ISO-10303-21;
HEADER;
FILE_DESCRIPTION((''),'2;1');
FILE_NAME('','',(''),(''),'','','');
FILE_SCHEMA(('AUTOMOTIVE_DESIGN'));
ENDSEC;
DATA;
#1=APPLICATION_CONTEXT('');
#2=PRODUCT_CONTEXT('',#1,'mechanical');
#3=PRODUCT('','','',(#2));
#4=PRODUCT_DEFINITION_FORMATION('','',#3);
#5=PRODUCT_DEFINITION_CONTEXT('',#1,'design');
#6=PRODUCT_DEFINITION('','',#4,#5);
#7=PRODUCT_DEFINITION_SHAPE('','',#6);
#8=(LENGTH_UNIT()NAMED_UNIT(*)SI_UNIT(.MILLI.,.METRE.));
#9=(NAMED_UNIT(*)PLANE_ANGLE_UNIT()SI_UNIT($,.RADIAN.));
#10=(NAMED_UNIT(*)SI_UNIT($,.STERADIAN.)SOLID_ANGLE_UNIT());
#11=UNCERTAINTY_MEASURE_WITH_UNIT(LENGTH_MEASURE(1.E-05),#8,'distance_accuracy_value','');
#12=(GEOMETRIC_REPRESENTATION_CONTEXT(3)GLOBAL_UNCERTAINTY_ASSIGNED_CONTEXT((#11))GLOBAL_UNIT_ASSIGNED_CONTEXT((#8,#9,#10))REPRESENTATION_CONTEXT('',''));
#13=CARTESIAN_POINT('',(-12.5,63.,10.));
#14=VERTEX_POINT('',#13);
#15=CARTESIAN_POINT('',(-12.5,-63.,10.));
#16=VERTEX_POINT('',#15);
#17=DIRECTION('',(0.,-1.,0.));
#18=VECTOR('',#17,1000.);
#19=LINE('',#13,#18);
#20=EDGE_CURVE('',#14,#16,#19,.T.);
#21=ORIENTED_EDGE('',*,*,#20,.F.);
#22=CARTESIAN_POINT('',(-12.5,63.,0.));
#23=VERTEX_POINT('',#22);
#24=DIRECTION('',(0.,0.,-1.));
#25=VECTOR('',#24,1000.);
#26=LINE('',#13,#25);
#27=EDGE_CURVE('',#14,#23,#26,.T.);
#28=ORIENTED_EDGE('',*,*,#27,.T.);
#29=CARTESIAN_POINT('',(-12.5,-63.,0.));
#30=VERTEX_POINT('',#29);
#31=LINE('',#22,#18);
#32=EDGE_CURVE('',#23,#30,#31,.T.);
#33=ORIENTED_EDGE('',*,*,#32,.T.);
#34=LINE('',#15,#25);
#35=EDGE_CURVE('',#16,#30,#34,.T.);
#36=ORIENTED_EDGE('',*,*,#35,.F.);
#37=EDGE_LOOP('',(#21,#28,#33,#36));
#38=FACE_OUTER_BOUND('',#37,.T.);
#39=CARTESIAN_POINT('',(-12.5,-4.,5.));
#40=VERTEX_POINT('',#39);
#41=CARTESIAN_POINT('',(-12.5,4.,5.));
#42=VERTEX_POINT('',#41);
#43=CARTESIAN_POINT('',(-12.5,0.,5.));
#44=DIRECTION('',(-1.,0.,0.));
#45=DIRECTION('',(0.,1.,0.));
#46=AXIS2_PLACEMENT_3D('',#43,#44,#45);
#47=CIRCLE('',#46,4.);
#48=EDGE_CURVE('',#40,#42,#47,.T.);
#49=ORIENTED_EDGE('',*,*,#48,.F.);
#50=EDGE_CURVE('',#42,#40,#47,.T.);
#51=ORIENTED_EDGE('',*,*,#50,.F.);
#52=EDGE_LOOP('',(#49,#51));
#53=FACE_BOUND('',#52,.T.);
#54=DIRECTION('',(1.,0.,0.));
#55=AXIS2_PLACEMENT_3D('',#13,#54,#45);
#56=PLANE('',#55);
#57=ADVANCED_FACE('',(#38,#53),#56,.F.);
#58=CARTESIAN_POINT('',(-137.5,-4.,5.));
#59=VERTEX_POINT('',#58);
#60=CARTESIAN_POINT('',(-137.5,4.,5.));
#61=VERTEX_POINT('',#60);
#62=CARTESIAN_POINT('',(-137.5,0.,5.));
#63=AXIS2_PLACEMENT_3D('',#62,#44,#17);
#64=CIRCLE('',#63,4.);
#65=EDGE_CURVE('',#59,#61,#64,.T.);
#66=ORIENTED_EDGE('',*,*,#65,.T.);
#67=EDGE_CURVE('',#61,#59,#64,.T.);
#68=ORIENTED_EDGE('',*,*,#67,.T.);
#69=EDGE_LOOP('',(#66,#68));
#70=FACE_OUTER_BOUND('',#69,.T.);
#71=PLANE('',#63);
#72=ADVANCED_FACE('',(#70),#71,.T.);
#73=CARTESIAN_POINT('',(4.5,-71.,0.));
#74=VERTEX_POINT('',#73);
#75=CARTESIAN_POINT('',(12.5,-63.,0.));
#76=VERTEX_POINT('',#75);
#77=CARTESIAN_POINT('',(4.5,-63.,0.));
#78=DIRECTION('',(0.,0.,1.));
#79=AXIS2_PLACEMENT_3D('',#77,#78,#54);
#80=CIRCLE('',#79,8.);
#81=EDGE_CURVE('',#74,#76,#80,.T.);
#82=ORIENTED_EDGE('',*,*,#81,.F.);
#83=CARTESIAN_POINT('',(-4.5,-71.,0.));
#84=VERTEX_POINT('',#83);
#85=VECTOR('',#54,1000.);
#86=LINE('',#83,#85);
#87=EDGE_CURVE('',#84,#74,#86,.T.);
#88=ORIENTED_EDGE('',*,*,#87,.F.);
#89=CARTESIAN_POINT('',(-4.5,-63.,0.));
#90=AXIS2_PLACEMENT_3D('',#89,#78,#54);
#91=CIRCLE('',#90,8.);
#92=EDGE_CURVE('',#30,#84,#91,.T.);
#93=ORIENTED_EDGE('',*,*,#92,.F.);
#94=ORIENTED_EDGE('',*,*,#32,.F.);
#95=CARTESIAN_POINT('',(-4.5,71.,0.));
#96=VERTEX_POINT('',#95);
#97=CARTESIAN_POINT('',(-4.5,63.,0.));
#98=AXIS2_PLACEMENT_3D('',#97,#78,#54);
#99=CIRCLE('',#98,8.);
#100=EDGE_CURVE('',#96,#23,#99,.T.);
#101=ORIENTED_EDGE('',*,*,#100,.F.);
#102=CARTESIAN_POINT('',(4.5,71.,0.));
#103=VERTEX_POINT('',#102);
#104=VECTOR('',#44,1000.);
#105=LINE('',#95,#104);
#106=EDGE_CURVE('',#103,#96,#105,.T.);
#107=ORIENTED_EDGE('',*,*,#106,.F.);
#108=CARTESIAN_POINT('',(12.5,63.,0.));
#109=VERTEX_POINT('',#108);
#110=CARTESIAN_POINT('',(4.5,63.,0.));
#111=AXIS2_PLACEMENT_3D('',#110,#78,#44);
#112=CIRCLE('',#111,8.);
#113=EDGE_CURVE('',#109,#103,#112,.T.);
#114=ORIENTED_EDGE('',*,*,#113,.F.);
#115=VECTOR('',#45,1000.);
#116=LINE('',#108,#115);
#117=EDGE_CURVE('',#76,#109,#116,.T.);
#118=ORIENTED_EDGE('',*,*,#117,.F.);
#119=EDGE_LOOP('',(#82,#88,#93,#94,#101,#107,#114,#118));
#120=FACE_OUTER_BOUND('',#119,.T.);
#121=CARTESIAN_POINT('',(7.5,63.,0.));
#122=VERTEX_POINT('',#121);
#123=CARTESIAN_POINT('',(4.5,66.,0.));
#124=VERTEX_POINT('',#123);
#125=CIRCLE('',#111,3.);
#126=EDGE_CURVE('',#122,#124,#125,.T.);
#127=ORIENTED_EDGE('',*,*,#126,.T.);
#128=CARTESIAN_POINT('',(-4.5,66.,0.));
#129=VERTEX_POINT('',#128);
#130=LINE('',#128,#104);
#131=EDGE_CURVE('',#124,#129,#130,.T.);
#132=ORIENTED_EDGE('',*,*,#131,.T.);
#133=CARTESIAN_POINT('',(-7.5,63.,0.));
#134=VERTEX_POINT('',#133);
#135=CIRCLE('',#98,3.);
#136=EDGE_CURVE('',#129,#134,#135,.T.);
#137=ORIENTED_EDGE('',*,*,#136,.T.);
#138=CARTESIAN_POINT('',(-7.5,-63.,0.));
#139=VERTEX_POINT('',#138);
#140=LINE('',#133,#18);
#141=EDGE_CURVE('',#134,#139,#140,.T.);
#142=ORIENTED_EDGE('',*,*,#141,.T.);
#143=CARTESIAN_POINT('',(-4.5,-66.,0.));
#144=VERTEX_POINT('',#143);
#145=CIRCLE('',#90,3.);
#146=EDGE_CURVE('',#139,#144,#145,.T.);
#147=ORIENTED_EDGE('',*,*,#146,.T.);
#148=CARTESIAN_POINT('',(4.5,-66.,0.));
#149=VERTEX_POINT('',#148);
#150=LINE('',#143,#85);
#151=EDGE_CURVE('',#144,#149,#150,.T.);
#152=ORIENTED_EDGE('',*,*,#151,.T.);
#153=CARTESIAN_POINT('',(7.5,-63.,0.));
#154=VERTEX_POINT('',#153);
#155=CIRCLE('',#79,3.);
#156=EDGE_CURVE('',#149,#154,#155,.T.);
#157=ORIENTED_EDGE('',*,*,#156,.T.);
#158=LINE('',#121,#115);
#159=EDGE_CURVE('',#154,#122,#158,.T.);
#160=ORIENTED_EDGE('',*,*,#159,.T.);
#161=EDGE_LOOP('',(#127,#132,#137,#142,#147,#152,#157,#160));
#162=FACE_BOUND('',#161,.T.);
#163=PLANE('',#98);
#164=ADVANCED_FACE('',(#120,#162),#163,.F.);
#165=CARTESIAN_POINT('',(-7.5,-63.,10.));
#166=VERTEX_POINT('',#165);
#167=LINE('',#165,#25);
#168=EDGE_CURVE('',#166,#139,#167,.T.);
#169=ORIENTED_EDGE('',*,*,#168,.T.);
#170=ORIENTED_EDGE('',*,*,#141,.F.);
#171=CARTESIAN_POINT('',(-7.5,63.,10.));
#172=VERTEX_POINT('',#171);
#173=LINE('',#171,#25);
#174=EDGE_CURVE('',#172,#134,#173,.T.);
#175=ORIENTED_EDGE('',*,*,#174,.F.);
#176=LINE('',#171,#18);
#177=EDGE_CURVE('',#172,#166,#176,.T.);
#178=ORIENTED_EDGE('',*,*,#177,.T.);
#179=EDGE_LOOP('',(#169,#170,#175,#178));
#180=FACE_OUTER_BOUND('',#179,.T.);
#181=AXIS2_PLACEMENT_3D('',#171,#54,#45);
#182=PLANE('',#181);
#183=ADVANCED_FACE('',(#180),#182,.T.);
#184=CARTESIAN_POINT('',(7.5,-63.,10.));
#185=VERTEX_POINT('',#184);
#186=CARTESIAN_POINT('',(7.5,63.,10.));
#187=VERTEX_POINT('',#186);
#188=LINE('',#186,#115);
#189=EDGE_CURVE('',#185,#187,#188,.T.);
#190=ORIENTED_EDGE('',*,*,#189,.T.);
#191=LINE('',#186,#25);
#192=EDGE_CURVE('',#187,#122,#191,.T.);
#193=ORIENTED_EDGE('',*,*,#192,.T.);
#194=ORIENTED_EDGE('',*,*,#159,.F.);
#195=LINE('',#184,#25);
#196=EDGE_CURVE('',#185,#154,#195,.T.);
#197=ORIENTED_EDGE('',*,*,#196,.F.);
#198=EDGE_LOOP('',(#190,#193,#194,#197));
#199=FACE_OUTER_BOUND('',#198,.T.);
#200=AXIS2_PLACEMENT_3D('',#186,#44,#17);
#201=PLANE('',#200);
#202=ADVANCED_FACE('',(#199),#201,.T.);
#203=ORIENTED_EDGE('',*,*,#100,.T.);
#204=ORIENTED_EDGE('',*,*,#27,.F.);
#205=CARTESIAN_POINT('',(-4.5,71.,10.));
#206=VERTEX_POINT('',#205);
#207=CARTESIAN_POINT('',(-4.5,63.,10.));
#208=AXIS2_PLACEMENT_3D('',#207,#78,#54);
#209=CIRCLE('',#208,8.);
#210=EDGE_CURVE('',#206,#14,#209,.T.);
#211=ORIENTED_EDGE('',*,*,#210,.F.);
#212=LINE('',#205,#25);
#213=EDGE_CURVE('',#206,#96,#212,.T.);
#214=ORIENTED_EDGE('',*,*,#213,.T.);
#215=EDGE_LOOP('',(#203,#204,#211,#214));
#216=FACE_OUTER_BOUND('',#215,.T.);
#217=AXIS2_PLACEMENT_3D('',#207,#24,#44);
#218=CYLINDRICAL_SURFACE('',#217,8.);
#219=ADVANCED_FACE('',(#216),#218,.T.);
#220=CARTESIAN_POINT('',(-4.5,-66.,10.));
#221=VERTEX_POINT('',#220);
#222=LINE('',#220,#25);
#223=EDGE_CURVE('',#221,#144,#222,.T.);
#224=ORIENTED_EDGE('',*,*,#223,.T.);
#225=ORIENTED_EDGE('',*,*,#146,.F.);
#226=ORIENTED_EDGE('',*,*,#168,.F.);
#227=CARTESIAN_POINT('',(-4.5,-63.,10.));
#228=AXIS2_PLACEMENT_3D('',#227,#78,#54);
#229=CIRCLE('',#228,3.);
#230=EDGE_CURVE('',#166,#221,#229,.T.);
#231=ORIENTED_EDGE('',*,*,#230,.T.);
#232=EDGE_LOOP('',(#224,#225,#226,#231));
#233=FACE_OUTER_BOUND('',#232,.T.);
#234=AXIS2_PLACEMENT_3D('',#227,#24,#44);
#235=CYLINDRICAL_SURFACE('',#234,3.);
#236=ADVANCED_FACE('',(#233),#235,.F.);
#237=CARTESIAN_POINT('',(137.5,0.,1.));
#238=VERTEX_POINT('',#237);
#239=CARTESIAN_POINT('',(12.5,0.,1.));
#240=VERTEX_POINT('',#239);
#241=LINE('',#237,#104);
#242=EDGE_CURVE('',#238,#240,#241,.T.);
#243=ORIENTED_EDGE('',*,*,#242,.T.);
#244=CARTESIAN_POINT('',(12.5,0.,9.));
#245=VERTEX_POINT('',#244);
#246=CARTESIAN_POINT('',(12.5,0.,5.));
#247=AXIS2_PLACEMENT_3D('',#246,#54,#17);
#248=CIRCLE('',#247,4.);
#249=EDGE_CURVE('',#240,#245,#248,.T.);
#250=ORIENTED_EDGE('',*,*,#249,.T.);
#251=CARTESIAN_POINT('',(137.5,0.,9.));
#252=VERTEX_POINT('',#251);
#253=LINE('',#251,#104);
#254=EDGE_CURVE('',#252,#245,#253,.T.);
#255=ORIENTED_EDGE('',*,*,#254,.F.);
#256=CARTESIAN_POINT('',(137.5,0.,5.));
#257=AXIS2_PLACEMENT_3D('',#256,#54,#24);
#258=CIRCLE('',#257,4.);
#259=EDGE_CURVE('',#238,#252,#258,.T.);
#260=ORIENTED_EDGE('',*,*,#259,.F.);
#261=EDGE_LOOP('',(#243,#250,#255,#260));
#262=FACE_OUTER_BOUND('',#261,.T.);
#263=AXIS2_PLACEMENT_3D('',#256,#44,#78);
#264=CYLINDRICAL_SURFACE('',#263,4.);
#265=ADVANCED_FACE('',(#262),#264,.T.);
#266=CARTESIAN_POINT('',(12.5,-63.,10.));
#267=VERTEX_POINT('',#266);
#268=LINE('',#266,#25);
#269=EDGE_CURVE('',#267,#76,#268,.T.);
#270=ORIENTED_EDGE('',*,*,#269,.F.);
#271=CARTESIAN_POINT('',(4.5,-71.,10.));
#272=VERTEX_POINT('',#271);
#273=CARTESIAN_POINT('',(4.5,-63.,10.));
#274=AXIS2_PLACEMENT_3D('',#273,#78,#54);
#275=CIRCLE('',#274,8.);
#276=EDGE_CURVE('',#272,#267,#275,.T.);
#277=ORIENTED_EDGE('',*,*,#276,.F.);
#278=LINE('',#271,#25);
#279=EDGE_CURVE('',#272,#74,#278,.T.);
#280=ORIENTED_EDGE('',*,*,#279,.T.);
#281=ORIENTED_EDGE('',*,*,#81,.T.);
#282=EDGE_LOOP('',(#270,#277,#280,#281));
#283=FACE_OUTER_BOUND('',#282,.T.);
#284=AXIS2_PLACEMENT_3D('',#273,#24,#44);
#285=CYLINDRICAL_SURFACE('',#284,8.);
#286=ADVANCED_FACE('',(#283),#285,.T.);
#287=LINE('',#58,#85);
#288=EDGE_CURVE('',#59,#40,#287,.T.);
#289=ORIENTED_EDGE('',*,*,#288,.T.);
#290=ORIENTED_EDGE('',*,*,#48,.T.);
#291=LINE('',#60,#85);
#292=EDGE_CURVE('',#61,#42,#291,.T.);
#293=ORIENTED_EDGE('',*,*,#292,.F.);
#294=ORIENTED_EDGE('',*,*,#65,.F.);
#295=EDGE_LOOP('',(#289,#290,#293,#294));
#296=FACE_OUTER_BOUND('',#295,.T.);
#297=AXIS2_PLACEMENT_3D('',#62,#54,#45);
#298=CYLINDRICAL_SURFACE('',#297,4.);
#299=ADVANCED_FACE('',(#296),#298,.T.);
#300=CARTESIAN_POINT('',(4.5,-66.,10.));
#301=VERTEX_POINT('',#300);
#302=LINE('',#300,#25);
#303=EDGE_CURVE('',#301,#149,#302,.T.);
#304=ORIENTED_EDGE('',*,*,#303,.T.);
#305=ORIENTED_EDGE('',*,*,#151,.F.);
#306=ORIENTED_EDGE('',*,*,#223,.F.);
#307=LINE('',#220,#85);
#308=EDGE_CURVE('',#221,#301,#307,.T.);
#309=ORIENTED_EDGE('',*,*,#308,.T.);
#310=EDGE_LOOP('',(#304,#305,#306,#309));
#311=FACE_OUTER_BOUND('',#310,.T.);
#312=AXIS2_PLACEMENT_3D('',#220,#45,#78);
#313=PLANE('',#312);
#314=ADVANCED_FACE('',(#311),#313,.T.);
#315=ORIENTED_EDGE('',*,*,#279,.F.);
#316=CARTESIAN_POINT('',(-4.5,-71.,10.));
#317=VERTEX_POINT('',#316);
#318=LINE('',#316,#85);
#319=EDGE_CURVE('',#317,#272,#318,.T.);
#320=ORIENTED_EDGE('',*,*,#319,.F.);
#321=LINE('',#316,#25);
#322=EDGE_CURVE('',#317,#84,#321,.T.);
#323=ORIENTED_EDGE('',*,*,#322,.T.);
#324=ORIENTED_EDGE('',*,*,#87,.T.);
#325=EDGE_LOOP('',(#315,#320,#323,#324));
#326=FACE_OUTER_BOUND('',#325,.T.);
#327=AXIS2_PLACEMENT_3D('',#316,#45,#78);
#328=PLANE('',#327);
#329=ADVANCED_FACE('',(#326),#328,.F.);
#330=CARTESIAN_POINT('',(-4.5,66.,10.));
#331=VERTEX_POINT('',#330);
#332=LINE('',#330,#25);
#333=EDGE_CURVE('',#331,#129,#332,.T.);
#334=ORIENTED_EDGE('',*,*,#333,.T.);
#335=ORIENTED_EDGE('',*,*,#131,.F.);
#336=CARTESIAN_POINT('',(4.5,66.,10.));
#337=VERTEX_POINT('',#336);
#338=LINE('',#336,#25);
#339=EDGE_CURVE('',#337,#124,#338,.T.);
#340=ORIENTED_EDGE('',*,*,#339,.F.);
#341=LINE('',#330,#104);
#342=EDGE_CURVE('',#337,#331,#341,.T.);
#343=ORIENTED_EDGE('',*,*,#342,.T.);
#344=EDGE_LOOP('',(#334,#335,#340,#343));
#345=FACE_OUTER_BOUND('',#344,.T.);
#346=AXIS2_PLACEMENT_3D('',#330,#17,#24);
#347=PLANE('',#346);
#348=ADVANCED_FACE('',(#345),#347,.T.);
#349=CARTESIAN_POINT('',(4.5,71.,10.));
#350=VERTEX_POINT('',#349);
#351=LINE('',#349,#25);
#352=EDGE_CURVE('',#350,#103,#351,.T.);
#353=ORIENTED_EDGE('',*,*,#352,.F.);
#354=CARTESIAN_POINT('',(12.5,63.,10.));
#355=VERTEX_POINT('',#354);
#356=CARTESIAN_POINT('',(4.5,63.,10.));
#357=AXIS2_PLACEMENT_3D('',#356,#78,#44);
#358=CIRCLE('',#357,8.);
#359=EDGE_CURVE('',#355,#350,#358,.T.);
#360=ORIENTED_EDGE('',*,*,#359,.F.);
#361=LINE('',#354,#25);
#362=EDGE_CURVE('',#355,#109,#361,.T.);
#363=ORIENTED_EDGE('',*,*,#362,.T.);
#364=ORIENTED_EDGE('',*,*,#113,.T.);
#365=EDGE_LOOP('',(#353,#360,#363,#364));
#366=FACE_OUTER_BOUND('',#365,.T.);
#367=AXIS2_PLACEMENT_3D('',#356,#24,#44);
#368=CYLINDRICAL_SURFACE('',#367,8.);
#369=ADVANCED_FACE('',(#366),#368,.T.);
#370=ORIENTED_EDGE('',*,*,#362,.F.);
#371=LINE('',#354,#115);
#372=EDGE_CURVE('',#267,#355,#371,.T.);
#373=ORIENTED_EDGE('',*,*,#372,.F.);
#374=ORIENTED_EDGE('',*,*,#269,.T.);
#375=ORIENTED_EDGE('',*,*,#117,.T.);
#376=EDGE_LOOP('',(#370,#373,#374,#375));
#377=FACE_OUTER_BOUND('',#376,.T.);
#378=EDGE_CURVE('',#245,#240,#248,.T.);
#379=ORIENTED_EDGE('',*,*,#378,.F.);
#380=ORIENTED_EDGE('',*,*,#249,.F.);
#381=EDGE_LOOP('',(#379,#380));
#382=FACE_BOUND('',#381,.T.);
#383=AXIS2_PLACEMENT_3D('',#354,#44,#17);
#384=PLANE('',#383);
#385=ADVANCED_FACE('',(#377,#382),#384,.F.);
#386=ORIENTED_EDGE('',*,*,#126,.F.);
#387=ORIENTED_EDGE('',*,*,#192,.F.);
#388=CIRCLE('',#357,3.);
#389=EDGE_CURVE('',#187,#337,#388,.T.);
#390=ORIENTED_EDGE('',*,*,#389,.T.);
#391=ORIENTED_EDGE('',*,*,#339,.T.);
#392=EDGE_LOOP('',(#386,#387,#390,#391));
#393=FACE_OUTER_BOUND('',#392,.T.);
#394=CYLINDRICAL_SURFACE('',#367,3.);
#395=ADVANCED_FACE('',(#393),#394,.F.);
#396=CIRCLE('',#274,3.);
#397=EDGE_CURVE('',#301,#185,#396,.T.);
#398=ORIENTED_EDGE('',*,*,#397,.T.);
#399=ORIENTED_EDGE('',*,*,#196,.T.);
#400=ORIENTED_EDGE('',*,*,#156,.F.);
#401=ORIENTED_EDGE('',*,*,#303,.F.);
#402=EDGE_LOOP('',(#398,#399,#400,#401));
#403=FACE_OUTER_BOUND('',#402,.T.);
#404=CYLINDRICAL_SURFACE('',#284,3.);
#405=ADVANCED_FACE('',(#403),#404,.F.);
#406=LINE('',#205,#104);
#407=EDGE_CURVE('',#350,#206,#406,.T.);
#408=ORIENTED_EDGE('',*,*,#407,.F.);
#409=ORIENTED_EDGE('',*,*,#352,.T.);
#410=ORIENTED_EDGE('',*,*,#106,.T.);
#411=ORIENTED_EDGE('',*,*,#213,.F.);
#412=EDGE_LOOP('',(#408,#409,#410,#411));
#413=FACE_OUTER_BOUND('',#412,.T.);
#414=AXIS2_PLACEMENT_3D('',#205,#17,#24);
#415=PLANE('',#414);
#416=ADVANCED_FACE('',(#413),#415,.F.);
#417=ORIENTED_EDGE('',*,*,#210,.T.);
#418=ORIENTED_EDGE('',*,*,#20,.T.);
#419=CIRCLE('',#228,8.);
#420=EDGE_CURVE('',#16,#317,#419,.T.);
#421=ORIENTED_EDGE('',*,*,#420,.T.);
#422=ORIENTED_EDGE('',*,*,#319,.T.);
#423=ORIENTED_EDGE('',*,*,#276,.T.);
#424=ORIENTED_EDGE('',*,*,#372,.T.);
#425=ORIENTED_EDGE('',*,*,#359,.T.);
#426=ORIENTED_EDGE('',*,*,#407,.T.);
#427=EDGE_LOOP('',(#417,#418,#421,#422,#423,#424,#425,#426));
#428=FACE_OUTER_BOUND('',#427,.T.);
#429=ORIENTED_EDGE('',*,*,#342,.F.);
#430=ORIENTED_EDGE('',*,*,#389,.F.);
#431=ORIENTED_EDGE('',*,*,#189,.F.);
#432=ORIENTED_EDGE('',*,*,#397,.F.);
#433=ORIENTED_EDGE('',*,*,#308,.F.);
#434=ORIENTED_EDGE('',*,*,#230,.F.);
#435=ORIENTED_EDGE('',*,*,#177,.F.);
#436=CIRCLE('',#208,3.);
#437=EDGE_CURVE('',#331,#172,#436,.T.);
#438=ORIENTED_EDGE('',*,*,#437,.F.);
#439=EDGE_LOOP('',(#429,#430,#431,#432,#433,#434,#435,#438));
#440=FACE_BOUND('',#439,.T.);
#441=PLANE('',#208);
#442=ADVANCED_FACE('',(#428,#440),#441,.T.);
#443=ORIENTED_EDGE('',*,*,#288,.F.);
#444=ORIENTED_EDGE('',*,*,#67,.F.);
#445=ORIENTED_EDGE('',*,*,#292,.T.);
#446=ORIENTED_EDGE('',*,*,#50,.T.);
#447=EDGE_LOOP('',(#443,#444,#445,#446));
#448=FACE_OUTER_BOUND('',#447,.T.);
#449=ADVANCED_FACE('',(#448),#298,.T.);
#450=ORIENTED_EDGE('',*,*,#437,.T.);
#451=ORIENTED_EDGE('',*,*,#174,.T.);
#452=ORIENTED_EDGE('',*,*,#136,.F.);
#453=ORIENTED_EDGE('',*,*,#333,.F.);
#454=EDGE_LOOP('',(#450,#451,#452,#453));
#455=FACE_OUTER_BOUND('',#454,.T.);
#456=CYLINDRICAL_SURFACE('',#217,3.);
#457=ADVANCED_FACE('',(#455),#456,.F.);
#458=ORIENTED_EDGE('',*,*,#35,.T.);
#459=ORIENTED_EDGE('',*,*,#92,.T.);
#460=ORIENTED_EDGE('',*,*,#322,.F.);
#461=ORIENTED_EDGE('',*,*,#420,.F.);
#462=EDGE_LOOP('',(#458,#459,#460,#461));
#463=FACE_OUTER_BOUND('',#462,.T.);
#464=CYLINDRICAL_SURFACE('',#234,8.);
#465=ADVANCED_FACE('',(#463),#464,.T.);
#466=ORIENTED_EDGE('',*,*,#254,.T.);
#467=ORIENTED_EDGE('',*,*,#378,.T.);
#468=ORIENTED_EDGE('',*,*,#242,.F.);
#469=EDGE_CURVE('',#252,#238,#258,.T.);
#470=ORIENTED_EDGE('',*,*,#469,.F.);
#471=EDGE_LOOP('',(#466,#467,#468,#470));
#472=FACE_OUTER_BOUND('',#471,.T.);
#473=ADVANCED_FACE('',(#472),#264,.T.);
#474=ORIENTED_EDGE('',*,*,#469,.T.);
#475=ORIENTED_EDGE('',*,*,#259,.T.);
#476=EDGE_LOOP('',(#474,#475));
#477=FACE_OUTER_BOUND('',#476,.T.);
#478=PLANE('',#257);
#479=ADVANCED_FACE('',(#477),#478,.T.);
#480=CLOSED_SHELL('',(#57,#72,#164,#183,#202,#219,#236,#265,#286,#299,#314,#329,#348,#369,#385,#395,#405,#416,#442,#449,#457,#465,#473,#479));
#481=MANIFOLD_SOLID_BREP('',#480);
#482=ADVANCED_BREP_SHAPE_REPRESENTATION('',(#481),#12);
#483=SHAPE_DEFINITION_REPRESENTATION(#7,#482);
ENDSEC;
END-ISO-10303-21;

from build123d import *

# Parameters (mm, degrees)
BOSS_EXTRUDE1_DEPTH = 10
SKETCH2_R           = 4
BOSS_EXTRUDE2_DEPTH = 125
BOSS_EXTRUDE3_START = 125
SKETCH3_R           = 4
BOSS_EXTRUDE3_DEPTH = 125


with BuildPart() as part:
    # Sketch1 → Boss-Extrude1 (new body)
    with BuildSketch(Plane.XY):
        with BuildLine():
            Line((-4.5, 71), (4.5, 71))
            ThreePointArc((4.5, 71), (10.156854249, 68.656854249), (12.5, 63))
            Line((12.5, 63), (12.5, -63))
            ThreePointArc((12.5, -63), (10.156854249, -68.656854249), (4.5, -71))
            Line((4.5, -71), (-4.5, -71))
            ThreePointArc((-4.5, -71), (-10.156854249, -68.656854249), (-12.5, -63))
            Line((-12.5, -63), (-12.5, 63))
            ThreePointArc((-12.5, 63), (-10.156854249, 68.656854249), (-4.5, 71))
        make_face()
        with BuildLine():
            Line((-4.5, 66), (4.5, 66))
            ThreePointArc((4.5, 66), (6.621320344, 65.121320344), (7.5, 63))
            Line((7.5, 63), (7.5, -63))
            ThreePointArc((7.5, -63), (6.621320344, -65.121320344), (4.5, -66))
            Line((4.5, -66), (-4.5, -66))
            ThreePointArc((-4.5, -66), (-6.621320344, -65.121320344), (-7.5, -63))
            Line((-7.5, -63), (-7.5, 63))
            ThreePointArc((-7.5, 63), (-6.621320344, 65.121320344), (-4.5, 66))
        make_face(mode=Mode.SUBTRACT)
    extrude(amount=BOSS_EXTRUDE1_DEPTH)

    # Sketch2 → Boss-Extrude2 (add)
    with BuildSketch(Plane(origin=(12.5, 0, 0), x_dir=(0, 0, -1), z_dir=(1, 0, 0))):
        with Locations(Location((-5, 0, 0), (0, 0, 270))):
            Circle(SKETCH2_R)
    extrude(amount=BOSS_EXTRUDE2_DEPTH)

    # Sketch3 → Boss-Extrude3 (add)
    with BuildSketch(Plane.ZY.offset(12.5).offset(BOSS_EXTRUDE3_START)):
        with Locations(Location((5, 0, 0), (0, 0, 270))):
            Circle(SKETCH3_R)
    extrude(amount=-BOSS_EXTRUDE3_DEPTH)


solid = part.part
